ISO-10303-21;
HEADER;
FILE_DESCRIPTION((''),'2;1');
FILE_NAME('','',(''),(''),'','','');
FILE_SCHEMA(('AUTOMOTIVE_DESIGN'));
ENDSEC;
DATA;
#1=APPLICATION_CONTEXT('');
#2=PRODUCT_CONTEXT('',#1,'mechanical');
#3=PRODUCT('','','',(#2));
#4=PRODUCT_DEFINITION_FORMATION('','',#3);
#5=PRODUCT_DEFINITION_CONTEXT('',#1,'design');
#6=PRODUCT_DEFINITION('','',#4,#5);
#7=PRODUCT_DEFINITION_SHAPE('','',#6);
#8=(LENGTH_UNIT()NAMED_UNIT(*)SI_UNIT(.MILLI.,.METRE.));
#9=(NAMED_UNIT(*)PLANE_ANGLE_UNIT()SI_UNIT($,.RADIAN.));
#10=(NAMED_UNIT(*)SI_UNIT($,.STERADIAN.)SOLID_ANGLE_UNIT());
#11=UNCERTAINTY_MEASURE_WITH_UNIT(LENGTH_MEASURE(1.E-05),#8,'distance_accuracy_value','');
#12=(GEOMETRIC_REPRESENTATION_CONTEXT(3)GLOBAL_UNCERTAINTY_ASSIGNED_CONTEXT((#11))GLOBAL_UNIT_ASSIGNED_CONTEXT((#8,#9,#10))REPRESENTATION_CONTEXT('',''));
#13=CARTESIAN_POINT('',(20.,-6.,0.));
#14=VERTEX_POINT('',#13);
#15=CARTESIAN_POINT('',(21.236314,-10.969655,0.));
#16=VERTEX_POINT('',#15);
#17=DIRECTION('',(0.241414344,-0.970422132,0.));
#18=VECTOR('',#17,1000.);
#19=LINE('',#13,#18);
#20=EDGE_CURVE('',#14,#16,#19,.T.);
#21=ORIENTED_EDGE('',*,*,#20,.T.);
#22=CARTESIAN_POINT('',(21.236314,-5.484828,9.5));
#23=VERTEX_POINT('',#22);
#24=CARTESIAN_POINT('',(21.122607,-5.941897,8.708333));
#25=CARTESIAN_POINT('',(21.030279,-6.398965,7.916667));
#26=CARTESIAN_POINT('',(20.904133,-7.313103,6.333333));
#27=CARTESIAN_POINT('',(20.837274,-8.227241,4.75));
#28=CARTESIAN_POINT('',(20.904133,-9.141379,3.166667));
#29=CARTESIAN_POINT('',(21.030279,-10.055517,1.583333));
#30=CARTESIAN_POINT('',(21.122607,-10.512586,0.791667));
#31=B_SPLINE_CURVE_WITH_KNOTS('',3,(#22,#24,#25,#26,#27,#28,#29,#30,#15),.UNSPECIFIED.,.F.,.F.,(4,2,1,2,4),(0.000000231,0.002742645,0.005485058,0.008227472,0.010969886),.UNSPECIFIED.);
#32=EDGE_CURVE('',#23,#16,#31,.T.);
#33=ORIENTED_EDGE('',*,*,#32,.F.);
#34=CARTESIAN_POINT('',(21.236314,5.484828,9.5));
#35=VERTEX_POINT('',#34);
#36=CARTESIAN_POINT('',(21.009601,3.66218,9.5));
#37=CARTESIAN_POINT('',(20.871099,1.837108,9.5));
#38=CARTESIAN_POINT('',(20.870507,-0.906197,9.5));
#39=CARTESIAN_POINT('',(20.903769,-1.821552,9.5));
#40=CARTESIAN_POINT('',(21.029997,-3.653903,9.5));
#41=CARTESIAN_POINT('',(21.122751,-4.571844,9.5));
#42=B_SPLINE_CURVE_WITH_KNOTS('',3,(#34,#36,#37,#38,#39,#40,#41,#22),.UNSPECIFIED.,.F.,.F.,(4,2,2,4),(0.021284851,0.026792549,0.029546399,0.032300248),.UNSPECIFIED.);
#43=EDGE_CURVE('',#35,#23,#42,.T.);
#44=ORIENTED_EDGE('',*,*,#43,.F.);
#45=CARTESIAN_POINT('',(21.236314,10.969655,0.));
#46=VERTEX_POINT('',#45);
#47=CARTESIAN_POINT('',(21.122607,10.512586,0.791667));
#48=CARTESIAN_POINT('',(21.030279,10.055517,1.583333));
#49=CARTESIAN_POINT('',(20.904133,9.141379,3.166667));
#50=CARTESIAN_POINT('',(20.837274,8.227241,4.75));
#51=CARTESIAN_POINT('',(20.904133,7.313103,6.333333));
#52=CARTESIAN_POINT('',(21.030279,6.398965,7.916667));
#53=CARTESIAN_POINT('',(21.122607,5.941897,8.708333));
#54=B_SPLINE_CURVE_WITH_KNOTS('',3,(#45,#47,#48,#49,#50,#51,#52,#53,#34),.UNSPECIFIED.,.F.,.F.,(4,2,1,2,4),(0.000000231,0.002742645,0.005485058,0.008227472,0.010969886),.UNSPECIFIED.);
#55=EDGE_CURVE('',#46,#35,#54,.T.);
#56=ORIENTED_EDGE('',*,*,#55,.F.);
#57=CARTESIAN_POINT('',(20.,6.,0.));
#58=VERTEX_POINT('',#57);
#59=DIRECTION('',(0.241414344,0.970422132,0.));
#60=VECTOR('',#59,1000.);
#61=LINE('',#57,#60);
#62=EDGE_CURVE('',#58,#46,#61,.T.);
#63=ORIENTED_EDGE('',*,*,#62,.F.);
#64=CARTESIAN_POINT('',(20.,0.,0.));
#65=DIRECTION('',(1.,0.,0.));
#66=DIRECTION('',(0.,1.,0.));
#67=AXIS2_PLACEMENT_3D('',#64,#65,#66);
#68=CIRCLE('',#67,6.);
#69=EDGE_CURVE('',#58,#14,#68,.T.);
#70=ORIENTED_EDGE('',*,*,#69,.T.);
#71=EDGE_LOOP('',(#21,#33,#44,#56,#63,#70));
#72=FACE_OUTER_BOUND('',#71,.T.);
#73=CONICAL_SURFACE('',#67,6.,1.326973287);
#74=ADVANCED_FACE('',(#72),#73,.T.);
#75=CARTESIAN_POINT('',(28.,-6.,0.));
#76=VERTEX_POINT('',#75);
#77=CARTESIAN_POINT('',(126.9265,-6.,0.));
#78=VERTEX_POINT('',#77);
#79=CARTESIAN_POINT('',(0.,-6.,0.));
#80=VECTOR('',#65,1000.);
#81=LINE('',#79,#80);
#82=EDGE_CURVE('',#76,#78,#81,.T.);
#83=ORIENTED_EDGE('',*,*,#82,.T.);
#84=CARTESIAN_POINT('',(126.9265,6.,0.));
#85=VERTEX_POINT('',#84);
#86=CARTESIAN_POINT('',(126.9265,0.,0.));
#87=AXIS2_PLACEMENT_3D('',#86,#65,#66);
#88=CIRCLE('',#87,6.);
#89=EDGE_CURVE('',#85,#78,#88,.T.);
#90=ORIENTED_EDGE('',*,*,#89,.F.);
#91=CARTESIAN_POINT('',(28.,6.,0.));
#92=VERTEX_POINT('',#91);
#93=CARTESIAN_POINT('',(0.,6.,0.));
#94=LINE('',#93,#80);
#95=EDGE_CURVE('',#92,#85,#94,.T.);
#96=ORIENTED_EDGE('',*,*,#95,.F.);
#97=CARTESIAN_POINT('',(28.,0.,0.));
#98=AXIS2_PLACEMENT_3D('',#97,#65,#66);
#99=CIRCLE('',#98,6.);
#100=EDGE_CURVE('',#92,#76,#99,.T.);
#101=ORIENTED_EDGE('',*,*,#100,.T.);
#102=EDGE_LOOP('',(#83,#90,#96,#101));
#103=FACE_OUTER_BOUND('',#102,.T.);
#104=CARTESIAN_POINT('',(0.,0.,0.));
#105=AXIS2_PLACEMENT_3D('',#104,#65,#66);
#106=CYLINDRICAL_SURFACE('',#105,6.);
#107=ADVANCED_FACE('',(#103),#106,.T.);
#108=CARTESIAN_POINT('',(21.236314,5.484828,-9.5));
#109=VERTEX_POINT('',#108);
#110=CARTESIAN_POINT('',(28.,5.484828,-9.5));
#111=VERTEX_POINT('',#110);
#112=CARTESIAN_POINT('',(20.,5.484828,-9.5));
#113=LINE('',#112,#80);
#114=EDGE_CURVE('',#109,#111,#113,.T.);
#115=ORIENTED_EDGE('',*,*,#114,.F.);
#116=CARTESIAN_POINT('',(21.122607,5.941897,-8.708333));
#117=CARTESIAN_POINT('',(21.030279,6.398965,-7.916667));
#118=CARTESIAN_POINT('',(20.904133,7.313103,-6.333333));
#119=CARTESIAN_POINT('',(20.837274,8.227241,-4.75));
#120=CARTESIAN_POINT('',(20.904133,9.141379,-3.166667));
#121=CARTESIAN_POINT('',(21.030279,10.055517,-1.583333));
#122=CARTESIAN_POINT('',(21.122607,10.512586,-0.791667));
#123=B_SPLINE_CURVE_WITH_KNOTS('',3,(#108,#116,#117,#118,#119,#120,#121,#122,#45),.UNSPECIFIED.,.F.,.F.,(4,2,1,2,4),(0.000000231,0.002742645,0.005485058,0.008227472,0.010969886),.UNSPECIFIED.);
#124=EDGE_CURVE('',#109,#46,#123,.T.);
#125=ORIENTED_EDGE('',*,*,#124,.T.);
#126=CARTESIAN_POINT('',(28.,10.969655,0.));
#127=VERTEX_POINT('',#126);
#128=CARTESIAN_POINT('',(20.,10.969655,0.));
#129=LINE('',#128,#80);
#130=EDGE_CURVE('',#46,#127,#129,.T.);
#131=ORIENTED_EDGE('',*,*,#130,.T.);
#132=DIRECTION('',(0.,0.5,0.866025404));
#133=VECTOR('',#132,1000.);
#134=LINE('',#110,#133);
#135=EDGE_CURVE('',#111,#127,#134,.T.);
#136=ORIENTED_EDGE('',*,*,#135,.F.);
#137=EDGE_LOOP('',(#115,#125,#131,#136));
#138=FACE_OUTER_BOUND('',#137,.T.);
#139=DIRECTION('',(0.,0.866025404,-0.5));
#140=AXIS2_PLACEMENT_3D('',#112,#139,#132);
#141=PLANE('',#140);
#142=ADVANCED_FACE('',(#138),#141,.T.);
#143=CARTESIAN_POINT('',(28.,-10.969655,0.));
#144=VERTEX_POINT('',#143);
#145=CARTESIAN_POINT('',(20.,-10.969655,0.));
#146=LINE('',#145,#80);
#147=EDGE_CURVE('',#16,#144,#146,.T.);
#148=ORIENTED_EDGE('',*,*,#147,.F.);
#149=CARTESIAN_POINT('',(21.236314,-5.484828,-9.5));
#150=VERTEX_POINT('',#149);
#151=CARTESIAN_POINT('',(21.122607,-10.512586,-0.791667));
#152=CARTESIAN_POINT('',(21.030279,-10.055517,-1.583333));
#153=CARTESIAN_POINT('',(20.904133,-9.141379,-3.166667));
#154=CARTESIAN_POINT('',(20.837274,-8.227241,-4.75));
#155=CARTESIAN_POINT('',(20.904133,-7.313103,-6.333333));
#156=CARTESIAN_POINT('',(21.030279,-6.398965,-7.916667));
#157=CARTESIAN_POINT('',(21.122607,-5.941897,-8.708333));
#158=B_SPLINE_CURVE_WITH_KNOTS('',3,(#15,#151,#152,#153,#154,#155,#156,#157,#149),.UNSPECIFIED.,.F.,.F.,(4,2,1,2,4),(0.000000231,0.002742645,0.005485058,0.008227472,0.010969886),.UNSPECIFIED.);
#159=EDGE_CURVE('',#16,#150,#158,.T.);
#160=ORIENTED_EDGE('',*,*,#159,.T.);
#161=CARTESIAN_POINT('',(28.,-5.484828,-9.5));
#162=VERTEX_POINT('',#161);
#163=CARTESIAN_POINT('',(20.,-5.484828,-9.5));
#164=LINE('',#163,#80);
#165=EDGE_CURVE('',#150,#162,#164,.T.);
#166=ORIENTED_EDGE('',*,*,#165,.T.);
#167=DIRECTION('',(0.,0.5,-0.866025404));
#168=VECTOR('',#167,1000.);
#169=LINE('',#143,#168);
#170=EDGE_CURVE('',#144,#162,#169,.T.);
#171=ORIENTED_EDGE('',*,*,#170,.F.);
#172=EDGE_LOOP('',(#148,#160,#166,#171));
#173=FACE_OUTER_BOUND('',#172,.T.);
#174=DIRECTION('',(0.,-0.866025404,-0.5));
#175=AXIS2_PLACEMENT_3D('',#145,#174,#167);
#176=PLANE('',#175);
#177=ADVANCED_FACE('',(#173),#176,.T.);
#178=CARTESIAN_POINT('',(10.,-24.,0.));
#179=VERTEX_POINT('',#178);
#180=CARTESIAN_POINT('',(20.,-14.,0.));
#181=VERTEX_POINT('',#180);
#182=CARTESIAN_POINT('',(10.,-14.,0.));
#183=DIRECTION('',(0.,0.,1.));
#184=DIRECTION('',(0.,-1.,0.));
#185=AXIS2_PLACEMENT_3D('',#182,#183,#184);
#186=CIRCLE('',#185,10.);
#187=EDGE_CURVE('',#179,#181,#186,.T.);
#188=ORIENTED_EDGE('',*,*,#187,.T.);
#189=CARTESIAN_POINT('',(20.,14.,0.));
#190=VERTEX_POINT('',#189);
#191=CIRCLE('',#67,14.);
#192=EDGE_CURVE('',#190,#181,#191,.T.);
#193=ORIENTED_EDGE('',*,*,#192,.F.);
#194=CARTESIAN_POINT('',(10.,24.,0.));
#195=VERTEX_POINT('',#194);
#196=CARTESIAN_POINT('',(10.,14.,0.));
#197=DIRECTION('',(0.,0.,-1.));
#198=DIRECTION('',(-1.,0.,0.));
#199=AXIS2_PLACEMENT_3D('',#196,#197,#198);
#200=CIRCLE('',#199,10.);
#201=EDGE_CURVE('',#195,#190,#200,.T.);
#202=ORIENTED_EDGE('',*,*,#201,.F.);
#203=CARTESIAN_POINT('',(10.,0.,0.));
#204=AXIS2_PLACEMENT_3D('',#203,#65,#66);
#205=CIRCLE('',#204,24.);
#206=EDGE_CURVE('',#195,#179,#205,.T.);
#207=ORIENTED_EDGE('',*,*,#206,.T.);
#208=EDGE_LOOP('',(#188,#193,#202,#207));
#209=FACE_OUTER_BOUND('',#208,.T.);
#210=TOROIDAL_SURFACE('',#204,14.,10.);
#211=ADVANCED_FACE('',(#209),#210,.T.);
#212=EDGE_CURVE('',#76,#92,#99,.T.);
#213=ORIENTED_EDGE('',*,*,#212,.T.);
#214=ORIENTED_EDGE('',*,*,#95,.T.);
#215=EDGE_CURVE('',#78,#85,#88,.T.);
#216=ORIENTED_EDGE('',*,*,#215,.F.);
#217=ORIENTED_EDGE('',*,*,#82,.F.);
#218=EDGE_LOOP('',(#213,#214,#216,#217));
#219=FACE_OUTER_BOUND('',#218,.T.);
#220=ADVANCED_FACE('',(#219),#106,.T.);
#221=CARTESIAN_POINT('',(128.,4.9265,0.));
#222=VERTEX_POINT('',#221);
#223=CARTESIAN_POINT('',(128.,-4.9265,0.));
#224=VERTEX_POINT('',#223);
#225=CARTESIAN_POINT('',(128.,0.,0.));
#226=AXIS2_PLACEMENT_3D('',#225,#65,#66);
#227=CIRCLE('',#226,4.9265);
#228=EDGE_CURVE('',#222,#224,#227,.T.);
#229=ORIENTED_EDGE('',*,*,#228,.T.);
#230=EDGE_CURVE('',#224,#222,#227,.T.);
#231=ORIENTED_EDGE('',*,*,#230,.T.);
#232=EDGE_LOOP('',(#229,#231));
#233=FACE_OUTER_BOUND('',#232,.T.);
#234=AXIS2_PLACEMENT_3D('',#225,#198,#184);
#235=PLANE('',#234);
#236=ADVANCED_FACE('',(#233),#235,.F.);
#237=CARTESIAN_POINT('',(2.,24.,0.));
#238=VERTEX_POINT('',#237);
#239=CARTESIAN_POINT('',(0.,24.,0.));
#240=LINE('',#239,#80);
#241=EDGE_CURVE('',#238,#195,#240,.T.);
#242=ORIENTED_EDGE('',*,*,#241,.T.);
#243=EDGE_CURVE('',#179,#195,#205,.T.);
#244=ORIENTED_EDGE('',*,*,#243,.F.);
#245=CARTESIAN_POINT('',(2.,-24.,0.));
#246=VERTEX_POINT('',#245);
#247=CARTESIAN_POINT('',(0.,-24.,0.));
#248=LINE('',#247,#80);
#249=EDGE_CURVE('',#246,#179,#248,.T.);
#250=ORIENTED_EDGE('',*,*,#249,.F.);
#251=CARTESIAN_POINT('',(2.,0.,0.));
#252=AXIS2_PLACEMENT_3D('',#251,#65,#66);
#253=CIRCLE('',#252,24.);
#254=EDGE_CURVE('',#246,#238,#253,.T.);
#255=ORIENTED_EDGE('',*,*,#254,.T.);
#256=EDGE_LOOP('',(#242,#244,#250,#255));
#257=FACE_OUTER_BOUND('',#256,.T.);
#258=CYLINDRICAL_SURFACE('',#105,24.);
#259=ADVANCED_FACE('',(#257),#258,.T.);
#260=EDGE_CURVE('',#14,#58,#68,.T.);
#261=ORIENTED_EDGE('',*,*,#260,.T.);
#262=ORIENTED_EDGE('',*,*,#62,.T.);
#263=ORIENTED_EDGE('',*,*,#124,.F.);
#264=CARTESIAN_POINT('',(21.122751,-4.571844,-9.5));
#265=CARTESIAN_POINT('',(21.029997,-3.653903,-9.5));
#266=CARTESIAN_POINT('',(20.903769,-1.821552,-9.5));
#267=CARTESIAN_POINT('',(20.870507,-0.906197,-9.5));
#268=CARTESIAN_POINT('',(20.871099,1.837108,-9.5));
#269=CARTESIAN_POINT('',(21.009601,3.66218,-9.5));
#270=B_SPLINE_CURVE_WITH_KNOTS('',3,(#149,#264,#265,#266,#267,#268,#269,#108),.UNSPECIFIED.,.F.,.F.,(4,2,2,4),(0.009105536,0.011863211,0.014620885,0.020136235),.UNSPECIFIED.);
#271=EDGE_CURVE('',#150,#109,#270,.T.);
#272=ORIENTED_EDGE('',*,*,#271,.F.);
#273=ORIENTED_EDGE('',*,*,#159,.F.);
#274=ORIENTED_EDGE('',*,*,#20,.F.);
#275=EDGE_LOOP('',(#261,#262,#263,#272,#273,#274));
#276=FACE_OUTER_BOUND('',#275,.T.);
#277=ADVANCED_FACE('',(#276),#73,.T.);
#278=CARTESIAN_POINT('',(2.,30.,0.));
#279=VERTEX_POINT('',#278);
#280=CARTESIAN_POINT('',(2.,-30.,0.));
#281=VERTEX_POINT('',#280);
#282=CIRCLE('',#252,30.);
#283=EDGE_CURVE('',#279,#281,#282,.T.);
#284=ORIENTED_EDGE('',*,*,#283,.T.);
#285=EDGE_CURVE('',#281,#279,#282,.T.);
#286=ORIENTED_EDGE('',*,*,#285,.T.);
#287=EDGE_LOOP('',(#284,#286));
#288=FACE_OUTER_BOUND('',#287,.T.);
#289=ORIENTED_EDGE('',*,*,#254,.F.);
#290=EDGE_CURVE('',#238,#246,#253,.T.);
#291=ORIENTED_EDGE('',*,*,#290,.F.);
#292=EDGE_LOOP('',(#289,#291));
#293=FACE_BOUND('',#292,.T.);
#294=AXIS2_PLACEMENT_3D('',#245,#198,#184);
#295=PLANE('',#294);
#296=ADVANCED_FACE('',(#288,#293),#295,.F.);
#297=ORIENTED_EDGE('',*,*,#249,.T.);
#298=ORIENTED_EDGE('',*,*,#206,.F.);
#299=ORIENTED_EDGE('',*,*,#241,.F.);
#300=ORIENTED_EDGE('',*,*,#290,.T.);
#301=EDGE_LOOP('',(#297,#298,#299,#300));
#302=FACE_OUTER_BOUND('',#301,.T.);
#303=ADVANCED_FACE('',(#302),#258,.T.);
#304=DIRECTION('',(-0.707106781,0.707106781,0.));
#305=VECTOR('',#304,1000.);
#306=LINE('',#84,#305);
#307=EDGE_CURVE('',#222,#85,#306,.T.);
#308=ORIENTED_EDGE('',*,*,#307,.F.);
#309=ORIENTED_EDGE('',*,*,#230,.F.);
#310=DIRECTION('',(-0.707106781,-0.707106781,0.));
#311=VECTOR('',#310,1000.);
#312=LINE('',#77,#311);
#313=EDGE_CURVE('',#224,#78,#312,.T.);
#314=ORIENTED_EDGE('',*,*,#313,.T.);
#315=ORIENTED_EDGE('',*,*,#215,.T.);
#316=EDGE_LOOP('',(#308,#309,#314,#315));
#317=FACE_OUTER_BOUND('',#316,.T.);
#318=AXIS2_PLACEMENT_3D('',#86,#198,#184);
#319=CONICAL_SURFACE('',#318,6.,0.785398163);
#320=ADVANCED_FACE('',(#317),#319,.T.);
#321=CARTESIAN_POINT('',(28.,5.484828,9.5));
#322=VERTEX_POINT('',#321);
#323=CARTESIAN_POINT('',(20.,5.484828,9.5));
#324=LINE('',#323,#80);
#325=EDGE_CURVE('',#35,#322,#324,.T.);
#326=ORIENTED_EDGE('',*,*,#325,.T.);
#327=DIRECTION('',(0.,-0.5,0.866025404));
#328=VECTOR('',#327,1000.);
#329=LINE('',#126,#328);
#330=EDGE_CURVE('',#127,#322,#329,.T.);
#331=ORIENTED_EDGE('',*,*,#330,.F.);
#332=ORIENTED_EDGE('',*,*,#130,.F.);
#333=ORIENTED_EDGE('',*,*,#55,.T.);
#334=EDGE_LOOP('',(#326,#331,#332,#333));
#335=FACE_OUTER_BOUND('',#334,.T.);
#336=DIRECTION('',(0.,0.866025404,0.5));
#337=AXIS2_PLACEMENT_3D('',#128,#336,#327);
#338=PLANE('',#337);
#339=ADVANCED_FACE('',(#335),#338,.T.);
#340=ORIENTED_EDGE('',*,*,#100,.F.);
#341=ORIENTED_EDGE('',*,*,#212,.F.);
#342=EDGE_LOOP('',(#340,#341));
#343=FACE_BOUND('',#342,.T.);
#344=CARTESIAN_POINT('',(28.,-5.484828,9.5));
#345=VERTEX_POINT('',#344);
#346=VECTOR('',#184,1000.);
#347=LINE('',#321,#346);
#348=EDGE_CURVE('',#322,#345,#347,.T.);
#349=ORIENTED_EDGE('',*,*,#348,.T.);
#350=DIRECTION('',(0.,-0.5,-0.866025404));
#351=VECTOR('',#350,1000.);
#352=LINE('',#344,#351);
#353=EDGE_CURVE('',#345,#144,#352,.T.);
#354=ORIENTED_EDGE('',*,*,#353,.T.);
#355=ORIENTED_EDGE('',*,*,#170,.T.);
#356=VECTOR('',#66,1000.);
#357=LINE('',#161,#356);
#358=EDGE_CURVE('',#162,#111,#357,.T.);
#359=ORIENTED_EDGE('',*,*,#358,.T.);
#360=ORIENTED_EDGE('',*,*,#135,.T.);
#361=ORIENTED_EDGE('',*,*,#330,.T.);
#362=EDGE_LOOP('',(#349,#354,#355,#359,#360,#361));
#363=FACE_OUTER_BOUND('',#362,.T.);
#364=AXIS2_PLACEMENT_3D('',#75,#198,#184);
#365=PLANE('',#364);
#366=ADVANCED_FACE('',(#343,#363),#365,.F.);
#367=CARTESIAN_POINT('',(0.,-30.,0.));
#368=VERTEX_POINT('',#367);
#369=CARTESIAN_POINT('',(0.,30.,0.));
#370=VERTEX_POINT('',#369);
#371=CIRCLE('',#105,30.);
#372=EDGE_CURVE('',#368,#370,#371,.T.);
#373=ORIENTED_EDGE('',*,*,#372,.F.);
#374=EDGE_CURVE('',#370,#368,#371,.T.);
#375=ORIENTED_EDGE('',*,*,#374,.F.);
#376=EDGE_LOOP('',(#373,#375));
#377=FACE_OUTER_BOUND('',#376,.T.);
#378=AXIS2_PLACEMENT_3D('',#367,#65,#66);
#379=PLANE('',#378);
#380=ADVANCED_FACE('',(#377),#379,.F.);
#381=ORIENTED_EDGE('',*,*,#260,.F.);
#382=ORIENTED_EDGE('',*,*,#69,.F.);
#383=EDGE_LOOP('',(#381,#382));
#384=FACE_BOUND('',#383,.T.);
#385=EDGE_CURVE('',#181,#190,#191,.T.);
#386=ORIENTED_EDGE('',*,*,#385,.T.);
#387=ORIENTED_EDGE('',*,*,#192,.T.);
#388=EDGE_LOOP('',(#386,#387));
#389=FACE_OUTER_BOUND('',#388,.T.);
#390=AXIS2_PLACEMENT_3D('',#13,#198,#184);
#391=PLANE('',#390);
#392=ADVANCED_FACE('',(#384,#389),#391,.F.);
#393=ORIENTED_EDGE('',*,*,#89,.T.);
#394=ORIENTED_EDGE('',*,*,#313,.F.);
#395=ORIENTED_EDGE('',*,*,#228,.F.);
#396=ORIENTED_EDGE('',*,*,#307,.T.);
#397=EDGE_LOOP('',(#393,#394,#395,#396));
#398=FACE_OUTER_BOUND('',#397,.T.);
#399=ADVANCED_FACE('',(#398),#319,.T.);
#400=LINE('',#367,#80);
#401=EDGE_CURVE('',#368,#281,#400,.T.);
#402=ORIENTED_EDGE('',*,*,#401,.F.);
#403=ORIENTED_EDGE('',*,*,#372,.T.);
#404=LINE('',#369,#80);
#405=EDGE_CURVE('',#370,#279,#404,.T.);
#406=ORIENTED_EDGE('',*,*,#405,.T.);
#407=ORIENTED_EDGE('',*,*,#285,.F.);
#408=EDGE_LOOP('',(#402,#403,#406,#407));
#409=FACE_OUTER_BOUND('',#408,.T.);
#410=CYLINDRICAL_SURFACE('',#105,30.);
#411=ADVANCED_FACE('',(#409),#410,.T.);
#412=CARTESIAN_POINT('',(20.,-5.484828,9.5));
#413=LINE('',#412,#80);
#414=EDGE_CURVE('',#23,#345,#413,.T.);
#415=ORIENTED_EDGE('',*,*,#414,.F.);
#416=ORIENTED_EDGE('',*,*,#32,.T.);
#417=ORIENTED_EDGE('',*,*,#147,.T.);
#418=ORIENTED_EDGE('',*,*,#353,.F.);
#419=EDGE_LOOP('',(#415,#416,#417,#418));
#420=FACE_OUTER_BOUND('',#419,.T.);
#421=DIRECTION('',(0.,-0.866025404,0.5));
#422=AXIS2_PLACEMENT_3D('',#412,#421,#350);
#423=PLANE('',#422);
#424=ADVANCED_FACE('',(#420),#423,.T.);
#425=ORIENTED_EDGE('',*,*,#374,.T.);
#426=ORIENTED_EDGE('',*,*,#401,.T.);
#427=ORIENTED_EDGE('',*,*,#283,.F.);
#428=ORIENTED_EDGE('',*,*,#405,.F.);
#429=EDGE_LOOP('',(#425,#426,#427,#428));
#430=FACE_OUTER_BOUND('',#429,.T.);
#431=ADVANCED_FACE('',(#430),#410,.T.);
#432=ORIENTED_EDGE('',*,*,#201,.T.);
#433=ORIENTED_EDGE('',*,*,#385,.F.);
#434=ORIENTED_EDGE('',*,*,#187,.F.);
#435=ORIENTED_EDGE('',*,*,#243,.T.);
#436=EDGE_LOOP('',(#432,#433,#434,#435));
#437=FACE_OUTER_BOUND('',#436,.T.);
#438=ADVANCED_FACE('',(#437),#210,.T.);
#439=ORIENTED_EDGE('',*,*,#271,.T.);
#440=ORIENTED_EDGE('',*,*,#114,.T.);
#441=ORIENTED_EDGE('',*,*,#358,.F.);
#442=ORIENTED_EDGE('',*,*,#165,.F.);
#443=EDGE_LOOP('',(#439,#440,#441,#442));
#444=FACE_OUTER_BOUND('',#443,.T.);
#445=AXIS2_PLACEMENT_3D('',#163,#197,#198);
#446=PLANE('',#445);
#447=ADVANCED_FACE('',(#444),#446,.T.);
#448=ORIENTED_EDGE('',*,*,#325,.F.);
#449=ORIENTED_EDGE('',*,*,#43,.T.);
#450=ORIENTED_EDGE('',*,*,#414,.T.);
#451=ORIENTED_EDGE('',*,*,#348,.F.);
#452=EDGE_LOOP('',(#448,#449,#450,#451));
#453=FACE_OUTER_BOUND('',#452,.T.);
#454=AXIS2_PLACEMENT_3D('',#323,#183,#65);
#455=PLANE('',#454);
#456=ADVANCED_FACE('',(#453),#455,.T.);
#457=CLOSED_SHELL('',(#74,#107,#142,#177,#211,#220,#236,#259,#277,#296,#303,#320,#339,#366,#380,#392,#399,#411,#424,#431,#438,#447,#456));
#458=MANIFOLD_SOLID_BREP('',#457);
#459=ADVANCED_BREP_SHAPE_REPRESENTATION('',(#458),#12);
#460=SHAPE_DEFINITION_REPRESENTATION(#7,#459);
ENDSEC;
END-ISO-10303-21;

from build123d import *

# Parameters (mm, degrees)
SKETCH_2_R          = 12.35
CUT_EXTRUDE_1_DEPTH = 8


with BuildPart() as part:
    # 草图1 → 旋转1 (revolve)
    with BuildSketch(Plane.XY, mode=Mode.PRIVATE) as revolve_1_sk:
        with BuildLine():
            Line((128, 0), (128, -4.9265))
            Line((128, -4.9265), (126.9265, -6))
            Line((126.9265, -6), (28, -6))
            Line((28, -6), (28, -11.875))
            Line((28, -11.875), (21.461538462, -11.875))
            Line((21.461538462, -11.875), (20, -6))
            Line((20, -6), (20, -14))
            ThreePointArc((20, -14), (17.071067812, -21.071067812), (10, -24))
            Line((10, -24), (2, -24))
            Line((2, -24), (2, -30))
            Line((2, -30), (0, -30))
            Line((0, -30), (0, 0))
            Line((0, 0), (128, 0))
        make_face()
    revolve(revolve_1_sk.sketch.rotate(Axis((0, 0, 0), (1, 0, 0)), 180), axis=Axis((0, 0, 0), (1, 0, 0)))

    # 草图2 → 切除-拉伸1 (cut)
    with BuildSketch(Plane(origin=(28, 0, 0), x_dir=(0, 0, -1), z_dir=(1, 0, 0))):
        Circle(SKETCH_2_R)
        Polygon((-9.5, 5.484827557), (-9.5, -5.484827557), (0, -10.969655115), (9.5, -5.484827557), (9.5, 5.484827557), (0, 10.969655115), align=None, mode=Mode.SUBTRACT)
    extrude(amount=-CUT_EXTRUDE_1_DEPTH, mode=Mode.SUBTRACT)


solid = part.part
